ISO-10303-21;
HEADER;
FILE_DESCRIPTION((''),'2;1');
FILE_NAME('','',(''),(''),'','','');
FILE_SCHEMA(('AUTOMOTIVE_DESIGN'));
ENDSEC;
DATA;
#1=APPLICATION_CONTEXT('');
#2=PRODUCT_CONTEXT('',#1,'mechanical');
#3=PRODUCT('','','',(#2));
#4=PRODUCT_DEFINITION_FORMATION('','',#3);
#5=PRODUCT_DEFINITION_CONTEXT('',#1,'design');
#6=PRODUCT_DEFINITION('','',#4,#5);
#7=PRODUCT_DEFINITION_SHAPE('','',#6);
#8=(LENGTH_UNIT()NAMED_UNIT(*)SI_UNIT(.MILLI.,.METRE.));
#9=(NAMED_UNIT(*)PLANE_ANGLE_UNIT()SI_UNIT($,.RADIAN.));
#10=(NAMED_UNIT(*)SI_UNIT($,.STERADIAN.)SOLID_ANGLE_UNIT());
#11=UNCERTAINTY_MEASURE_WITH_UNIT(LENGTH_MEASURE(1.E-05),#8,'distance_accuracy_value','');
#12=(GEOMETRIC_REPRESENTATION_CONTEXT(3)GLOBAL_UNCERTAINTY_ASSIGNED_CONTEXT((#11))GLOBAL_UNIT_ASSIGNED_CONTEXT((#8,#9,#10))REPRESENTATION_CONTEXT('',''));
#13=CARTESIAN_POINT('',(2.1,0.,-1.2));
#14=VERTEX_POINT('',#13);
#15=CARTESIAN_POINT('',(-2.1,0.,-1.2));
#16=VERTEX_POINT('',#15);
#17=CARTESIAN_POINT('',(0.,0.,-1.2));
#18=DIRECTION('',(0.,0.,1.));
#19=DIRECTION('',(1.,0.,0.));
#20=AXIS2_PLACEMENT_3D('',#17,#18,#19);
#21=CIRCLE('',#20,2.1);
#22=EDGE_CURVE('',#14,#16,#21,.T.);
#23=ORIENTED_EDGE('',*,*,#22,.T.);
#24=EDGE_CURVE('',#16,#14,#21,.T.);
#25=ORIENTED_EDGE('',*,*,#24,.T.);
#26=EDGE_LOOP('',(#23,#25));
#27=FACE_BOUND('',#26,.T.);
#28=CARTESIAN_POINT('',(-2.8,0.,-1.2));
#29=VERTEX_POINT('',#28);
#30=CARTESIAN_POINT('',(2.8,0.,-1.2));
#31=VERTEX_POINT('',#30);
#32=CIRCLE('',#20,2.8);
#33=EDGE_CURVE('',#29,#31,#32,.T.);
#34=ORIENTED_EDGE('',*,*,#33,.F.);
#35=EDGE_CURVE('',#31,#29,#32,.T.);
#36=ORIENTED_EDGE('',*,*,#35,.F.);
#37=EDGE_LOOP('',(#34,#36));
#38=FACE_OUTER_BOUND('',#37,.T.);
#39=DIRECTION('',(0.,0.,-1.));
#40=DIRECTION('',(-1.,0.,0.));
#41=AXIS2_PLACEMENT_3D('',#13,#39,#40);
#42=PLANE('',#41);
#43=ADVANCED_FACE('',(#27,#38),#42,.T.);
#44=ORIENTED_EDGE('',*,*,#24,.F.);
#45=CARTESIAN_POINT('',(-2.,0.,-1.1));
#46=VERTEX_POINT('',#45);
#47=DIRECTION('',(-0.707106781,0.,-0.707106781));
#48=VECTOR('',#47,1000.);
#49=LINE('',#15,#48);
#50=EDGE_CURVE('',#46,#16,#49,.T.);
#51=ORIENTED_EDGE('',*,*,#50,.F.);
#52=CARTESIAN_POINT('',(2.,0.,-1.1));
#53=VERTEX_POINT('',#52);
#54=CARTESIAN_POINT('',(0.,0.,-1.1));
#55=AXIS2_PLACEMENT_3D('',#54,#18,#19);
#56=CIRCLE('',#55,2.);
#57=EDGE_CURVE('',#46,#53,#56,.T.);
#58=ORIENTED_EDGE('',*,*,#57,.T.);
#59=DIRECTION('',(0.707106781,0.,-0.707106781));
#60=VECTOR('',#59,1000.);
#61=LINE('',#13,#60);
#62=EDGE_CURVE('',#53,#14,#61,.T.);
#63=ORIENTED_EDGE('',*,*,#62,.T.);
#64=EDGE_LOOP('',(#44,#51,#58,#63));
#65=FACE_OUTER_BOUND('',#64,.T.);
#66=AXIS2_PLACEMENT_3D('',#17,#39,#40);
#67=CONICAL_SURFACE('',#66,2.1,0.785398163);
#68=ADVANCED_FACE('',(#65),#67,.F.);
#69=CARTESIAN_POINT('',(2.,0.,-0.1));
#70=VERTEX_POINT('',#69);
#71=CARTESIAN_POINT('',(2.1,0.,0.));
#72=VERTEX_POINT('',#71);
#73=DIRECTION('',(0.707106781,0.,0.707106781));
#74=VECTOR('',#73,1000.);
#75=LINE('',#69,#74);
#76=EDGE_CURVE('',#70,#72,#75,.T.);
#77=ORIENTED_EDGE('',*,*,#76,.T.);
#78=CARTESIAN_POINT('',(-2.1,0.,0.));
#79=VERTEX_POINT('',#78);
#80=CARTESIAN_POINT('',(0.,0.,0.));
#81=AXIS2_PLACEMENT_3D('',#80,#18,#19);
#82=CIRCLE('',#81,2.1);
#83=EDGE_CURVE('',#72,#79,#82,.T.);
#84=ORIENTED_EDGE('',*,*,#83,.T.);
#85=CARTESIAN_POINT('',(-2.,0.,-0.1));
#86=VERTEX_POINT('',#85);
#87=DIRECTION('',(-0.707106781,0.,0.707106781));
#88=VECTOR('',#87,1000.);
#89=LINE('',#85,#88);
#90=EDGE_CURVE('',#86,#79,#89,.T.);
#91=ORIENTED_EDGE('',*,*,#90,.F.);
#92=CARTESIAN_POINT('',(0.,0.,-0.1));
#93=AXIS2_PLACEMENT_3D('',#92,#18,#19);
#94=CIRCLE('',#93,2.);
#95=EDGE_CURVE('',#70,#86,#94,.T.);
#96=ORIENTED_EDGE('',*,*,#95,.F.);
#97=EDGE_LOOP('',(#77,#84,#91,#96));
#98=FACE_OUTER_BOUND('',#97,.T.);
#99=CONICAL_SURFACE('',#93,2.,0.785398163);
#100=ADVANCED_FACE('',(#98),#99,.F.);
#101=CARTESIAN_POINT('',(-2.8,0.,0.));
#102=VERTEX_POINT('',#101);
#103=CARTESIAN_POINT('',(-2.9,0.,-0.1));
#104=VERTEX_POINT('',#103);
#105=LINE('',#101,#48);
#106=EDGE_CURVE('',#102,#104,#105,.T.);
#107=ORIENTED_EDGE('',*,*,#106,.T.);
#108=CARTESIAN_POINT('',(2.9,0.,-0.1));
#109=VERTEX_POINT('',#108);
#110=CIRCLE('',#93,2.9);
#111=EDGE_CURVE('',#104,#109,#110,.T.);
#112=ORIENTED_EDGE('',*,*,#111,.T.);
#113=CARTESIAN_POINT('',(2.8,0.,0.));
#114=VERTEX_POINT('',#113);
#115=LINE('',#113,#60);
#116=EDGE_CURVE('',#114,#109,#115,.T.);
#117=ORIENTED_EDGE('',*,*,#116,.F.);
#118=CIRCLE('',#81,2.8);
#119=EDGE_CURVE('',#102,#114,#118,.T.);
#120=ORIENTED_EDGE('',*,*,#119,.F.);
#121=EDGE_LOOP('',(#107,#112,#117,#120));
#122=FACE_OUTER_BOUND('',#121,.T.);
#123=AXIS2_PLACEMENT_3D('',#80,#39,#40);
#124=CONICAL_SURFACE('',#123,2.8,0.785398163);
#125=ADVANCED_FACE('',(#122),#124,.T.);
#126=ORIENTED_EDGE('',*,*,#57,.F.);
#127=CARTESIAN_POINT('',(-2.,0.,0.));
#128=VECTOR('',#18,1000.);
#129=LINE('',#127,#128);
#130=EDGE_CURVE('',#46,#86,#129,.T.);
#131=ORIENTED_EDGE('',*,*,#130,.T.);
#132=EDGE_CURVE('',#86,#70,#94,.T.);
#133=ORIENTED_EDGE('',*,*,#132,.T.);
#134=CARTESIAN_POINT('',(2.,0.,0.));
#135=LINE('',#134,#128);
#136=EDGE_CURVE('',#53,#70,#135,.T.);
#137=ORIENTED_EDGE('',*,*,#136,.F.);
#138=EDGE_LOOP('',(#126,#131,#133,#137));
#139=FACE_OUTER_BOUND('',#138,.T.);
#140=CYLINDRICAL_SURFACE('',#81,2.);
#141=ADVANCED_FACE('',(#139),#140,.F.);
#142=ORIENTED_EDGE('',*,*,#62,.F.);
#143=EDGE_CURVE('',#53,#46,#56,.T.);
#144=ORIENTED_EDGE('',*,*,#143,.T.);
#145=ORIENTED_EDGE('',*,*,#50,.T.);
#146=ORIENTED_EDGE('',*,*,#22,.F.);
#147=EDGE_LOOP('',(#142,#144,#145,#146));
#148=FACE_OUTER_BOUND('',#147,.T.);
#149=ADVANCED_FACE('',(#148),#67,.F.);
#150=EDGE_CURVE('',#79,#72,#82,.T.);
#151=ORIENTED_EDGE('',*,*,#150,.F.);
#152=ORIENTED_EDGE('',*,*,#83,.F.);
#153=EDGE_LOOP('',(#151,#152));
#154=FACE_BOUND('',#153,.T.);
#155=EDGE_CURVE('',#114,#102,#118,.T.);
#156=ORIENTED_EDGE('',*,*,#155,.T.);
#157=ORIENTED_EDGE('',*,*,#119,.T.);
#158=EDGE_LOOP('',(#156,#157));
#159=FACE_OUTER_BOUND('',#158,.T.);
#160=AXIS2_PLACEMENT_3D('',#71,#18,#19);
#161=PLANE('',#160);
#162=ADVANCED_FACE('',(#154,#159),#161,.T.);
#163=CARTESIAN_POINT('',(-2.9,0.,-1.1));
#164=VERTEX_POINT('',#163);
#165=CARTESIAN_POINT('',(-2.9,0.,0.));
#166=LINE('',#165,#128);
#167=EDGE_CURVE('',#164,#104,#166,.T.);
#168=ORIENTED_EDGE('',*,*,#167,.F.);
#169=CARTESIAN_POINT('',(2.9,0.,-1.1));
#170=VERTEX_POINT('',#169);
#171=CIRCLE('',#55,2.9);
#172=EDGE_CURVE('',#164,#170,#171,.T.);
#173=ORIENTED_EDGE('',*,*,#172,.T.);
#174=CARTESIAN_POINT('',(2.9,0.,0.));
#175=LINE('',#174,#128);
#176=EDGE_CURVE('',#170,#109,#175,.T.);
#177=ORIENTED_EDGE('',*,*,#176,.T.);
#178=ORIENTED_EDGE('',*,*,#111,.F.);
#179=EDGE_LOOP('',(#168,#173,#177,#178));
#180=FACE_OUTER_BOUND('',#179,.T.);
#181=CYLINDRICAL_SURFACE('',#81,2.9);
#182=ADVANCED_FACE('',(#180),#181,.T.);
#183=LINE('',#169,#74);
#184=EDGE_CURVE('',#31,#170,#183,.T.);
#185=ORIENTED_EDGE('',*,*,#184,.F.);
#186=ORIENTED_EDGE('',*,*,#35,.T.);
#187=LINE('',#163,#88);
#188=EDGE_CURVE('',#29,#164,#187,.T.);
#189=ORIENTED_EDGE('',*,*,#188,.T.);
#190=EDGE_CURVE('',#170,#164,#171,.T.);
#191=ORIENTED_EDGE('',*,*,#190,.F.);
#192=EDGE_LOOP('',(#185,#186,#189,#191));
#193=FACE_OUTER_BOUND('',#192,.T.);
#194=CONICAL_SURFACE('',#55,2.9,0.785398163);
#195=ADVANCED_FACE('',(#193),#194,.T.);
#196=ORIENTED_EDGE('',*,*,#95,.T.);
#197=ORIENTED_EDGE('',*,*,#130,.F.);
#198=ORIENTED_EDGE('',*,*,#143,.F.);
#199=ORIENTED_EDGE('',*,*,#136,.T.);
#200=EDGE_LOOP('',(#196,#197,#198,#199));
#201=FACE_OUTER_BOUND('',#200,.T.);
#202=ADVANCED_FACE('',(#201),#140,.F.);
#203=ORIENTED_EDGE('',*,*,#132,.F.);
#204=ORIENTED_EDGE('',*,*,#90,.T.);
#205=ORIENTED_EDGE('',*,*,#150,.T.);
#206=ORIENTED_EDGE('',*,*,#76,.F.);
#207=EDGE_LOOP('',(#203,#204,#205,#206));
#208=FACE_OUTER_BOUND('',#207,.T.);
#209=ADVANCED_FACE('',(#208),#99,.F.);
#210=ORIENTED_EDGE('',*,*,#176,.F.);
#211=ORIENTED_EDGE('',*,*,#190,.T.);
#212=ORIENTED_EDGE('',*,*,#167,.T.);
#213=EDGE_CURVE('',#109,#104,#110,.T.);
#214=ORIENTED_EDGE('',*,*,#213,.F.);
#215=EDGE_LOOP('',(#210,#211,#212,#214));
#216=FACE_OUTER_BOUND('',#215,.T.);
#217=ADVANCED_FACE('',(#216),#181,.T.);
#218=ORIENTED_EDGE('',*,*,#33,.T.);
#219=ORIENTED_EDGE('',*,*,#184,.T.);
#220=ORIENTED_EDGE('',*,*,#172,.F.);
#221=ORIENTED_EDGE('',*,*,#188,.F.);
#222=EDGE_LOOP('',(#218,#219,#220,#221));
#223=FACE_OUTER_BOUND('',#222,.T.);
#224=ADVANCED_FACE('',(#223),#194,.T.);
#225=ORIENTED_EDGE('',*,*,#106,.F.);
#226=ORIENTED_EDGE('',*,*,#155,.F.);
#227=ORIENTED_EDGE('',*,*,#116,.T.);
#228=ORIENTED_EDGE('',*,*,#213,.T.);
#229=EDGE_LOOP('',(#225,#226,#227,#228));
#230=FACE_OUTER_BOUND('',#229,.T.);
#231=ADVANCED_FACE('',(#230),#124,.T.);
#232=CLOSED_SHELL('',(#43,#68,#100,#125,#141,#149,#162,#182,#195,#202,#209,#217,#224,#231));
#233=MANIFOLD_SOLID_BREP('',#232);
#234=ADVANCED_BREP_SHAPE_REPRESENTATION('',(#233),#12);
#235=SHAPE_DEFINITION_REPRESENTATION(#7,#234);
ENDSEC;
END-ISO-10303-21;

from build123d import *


with BuildPart() as part:
    # Sketch1 → Revolve1 (revolve)
    with BuildSketch(Plane(origin=(0, 0, 0), x_dir=(1, 0, 0), z_dir=(0, 1, 0))):
        Polygon((2.1, 0), (2.8, 0), (2.9, 0.1), (2.9, 1.1), (2.8, 1.2), (2.1, 1.2), (2, 1.1), (2, 0.1), align=None)
    revolve(axis=Axis((0, 0, 0), (0, 0, -1)))


solid = part.part
